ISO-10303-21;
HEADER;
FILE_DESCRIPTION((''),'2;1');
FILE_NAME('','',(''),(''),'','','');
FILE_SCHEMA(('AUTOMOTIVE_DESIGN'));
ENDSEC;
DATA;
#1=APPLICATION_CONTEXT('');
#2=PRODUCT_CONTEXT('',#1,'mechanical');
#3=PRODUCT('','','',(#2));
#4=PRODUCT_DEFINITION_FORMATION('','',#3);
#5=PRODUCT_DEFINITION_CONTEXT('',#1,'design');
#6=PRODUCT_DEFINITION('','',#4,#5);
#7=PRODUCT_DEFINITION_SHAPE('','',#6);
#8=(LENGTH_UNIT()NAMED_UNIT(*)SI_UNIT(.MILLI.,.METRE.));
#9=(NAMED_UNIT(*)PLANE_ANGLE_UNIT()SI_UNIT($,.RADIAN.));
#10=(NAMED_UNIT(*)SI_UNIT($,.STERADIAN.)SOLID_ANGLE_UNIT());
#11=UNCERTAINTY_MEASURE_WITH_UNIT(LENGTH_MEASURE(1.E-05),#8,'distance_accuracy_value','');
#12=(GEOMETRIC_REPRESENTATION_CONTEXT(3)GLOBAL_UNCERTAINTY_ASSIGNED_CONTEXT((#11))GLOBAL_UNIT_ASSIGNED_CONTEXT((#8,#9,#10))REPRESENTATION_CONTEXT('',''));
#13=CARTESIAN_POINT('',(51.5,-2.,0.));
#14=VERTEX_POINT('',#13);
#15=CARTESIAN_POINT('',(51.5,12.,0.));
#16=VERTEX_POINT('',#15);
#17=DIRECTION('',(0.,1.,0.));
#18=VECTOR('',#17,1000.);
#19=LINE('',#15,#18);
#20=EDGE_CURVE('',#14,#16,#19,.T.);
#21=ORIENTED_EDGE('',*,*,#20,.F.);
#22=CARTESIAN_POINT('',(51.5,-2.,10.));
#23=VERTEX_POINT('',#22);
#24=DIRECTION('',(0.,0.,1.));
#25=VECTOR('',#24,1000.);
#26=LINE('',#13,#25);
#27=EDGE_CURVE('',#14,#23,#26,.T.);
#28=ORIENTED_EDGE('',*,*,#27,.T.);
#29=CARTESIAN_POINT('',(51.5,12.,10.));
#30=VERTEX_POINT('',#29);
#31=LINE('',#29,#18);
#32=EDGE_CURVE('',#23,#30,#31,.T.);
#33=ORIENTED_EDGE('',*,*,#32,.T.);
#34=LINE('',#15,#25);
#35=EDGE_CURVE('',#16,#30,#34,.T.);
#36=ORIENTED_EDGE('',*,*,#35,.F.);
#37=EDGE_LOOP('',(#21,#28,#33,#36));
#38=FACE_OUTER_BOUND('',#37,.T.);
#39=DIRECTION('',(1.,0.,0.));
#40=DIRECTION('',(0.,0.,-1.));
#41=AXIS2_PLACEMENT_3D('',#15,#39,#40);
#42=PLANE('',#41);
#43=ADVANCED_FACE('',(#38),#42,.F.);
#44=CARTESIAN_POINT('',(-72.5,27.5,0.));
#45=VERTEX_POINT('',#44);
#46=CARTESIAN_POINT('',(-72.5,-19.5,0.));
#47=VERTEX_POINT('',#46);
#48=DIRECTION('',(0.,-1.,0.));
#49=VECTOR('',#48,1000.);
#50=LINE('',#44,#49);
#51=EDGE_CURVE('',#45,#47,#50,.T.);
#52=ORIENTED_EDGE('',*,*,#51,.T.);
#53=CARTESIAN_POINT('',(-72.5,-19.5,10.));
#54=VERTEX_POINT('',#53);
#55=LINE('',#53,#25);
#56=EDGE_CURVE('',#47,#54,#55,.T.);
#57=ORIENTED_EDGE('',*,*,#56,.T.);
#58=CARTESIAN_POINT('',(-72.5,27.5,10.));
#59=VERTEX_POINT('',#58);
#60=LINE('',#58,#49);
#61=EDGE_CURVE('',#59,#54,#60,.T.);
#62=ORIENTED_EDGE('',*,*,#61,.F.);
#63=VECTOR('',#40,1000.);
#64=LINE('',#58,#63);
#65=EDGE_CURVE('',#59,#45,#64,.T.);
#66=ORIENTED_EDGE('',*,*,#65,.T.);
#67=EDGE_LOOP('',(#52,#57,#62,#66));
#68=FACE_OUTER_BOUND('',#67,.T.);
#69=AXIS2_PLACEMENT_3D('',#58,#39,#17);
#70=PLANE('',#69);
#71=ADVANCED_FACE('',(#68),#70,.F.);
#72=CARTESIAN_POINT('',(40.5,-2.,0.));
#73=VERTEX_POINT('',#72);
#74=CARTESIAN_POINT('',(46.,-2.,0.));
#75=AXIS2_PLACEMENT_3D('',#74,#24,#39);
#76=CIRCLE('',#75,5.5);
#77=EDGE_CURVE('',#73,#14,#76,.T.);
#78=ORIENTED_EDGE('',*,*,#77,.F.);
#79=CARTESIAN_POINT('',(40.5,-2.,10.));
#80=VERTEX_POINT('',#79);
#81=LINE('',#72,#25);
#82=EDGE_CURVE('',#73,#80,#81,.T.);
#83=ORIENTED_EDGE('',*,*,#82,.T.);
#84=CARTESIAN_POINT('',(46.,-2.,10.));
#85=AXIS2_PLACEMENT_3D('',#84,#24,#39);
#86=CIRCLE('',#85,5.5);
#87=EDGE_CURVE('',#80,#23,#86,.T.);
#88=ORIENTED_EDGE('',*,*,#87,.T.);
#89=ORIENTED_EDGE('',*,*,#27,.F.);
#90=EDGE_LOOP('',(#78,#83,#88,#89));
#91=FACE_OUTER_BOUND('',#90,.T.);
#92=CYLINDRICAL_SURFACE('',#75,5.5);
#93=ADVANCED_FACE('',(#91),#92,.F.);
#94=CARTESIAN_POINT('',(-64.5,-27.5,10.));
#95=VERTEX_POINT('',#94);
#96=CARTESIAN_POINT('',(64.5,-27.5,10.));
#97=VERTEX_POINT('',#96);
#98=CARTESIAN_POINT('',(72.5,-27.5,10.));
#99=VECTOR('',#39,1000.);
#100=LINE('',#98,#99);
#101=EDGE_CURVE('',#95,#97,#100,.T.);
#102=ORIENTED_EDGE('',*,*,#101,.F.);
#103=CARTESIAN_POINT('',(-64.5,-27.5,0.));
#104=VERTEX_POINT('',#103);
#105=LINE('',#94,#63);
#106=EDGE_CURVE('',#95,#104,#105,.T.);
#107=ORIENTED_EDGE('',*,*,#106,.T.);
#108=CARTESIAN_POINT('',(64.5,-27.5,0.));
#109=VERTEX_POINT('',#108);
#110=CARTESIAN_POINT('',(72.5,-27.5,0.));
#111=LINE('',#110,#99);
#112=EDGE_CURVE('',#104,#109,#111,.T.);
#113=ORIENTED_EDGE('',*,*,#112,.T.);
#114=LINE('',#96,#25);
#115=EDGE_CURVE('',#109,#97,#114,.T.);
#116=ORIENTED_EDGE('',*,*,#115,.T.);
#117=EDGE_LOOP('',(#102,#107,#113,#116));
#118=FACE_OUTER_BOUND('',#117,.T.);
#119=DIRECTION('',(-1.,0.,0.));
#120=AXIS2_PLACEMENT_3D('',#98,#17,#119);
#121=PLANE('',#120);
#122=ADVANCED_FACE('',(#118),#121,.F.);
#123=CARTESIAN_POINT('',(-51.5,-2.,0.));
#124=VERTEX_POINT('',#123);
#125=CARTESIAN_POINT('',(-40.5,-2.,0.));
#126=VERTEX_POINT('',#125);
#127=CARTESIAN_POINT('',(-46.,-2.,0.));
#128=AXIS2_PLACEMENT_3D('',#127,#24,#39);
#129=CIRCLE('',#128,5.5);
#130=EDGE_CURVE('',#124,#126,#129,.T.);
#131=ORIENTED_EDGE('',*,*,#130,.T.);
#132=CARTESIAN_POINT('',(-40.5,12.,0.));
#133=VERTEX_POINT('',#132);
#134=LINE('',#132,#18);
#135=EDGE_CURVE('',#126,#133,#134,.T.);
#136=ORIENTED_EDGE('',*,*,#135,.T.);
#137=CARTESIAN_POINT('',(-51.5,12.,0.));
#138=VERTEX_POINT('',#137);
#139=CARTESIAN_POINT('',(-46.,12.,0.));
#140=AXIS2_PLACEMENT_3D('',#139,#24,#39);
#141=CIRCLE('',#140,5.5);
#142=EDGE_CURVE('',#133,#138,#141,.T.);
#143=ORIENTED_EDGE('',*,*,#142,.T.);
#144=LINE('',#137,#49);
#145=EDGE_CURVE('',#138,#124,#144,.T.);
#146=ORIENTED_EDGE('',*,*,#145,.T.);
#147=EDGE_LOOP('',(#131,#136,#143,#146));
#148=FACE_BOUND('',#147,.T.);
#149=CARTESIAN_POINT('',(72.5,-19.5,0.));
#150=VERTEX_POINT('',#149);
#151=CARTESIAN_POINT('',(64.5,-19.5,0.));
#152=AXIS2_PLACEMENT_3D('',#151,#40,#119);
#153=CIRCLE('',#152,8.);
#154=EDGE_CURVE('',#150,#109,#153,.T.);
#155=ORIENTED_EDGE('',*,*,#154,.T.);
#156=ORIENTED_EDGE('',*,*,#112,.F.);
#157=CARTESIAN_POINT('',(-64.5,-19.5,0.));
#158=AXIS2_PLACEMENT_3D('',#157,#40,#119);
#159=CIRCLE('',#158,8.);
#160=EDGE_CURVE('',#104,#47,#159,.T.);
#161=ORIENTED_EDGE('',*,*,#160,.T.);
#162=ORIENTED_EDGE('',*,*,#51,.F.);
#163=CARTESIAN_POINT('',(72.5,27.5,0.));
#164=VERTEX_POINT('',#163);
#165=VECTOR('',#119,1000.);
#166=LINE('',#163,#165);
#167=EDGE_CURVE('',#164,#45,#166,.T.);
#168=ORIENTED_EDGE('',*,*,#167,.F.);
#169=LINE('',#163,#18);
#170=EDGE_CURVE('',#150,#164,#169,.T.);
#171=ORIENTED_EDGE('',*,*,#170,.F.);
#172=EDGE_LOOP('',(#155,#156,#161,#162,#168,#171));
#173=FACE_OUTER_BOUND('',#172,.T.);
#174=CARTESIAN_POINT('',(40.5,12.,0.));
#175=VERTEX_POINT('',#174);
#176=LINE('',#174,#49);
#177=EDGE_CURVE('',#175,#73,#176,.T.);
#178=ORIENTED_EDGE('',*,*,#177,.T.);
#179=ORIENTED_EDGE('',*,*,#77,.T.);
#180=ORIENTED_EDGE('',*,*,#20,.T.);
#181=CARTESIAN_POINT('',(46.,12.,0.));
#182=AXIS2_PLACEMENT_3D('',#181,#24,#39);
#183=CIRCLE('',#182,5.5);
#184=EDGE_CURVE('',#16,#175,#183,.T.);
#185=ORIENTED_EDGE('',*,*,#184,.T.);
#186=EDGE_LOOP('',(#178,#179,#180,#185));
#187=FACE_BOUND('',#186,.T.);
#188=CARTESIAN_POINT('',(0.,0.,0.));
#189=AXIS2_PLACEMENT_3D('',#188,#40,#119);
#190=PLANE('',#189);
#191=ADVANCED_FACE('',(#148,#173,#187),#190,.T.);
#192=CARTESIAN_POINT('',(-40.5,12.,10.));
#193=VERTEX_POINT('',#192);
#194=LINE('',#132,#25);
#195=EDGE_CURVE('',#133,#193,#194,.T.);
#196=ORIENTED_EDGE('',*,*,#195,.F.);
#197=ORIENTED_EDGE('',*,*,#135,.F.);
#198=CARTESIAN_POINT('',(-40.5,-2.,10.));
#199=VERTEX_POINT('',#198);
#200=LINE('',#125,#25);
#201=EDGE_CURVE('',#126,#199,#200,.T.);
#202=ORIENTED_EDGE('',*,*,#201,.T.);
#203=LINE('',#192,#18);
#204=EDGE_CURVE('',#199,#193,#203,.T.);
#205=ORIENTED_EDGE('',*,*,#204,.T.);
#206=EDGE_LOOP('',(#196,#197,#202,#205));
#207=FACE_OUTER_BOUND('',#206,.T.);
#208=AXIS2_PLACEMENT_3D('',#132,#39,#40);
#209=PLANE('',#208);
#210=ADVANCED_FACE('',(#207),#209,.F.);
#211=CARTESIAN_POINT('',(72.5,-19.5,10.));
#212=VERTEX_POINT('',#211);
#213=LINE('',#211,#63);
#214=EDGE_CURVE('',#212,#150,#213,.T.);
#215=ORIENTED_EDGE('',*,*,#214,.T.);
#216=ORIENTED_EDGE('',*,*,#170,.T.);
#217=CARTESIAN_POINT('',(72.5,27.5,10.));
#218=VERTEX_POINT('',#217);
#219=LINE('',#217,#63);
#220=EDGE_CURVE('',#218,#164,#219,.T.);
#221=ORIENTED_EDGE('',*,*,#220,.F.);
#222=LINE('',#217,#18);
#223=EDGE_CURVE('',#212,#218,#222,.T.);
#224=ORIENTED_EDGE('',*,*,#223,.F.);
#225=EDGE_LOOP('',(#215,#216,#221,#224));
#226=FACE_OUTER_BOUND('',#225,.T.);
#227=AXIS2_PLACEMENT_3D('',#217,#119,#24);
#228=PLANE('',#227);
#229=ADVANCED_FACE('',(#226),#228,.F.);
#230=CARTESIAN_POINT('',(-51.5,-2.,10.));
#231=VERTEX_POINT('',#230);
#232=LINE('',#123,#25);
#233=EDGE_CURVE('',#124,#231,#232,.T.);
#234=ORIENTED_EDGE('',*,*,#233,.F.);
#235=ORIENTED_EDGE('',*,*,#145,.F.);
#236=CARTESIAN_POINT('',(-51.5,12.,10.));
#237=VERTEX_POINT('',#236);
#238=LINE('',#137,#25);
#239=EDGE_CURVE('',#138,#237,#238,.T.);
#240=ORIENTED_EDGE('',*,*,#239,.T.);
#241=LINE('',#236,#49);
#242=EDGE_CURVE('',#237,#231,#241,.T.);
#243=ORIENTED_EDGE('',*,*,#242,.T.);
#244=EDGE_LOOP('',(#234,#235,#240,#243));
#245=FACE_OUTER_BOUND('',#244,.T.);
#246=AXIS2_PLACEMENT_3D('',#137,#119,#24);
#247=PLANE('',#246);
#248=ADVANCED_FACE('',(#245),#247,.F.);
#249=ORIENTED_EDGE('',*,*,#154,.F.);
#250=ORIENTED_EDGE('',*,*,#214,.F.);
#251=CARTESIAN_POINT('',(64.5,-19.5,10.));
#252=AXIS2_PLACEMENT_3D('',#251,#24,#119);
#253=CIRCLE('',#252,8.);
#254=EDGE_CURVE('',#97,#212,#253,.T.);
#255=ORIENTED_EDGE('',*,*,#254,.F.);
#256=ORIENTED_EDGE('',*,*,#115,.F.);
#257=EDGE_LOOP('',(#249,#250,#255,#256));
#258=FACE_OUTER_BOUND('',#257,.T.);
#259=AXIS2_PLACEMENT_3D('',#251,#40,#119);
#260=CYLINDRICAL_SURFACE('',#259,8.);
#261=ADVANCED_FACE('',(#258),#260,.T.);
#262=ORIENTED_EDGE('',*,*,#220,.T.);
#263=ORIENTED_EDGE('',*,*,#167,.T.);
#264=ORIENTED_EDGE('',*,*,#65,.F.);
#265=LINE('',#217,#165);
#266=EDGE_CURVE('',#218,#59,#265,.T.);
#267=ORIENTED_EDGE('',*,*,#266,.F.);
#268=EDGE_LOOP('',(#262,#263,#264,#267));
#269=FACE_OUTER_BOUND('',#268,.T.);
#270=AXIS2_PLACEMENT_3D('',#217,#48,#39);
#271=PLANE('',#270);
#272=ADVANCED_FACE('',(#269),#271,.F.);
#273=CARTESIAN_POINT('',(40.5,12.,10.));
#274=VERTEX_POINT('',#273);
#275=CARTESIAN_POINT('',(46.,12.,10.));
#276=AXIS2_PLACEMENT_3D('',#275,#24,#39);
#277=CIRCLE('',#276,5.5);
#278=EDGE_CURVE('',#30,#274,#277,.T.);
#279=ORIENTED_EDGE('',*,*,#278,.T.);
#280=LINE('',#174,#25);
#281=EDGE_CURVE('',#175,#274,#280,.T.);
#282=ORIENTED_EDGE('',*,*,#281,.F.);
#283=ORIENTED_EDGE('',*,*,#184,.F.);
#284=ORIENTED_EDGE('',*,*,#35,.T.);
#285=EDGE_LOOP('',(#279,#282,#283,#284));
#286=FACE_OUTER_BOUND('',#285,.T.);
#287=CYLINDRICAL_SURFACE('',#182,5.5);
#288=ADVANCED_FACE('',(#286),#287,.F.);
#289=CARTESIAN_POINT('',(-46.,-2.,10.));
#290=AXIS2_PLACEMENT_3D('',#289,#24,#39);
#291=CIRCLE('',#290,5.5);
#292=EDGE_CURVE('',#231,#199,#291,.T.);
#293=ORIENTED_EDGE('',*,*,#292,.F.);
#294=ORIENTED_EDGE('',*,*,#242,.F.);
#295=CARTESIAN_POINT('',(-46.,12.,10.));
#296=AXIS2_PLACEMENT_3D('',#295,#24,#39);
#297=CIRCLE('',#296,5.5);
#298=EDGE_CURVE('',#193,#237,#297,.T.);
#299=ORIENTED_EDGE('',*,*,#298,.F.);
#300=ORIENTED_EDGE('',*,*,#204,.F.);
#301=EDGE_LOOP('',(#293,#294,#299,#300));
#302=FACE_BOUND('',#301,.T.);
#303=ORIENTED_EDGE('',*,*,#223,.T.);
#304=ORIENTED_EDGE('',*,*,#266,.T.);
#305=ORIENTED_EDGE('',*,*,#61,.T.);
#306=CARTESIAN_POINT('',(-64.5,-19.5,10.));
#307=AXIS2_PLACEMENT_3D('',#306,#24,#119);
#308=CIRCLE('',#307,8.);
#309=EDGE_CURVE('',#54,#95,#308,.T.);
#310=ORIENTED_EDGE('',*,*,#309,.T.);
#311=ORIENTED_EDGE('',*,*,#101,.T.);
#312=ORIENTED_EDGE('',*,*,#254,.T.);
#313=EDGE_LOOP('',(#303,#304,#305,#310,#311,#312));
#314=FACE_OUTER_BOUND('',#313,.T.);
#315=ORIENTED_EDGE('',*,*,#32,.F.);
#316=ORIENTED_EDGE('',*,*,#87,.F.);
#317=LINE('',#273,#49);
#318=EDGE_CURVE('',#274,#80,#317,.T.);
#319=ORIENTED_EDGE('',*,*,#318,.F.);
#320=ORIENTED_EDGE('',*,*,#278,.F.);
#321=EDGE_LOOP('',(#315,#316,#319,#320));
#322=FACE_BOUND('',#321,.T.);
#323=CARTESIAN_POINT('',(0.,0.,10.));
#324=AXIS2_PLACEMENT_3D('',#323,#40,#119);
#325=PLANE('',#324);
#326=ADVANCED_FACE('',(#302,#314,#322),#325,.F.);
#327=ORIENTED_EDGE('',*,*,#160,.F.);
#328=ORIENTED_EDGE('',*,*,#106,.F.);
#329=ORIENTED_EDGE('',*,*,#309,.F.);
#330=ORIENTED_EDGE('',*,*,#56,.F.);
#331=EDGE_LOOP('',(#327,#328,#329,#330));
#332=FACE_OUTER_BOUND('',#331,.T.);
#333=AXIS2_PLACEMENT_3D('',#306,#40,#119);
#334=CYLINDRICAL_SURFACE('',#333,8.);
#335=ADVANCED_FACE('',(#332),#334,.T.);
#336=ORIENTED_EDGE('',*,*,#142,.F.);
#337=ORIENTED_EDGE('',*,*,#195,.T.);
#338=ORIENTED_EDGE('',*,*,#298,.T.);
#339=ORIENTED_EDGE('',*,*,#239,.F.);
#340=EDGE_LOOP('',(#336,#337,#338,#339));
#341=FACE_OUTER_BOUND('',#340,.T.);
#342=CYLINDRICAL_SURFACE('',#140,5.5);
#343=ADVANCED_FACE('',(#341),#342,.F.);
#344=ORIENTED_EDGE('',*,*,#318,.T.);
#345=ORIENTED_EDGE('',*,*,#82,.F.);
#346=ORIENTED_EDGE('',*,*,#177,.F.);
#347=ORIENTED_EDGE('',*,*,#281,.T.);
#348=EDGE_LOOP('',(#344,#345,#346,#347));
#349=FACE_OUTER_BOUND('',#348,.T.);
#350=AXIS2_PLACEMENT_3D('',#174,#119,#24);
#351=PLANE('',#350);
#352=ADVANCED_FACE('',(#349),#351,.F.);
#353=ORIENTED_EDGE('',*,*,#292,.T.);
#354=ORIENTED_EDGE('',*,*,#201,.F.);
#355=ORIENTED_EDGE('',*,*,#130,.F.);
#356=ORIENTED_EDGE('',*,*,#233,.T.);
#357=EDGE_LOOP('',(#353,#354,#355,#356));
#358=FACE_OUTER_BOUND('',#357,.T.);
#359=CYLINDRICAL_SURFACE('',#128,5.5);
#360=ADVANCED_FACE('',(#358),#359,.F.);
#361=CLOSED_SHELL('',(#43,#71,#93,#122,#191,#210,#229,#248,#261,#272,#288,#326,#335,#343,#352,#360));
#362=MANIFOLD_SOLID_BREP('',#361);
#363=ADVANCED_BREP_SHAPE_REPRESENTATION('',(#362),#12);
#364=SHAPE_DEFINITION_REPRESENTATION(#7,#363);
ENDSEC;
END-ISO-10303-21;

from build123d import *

# Parameters (mm, degrees)
SKETCH_1_W          = 145
SKETCH_1_H          = 55
EXTRUDE_1_DEPTH     = 10
FILLET_1_R          = 8
CUT_EXTRUDE_1_DEPTH = 10


with BuildPart() as part:
    # 草图1 → 凸台-拉伸1 (new body)
    with BuildSketch(Plane.XY):
        Rectangle(SKETCH_1_W, SKETCH_1_H)
    extrude(amount=EXTRUDE_1_DEPTH)

    # 圆角1
    fillet_1_edges = [part.edges().sort_by_distance(p)[0] for p in [
        (72.5, -27.5, 5),
        (-72.5, -27.5, 5),
    ]]
    fillet(fillet_1_edges, radius=FILLET_1_R)

    # 草图2 → 切除-拉伸1 (cut)
    with BuildSketch(Plane.XY.offset(10)):
        with BuildLine():
            Line((51.5, 12), (51.5, -2))
            ThreePointArc((51.5, -2), (46, -7.5), (40.5, -2))
            Line((40.5, -2), (40.5, 12))
            ThreePointArc((40.5, 12), (46, 17.5), (51.5, 12))
        make_face()
        with BuildLine():
            Line((-40.5, 12), (-40.5, -2))
            ThreePointArc((-40.5, -2), (-46, -7.5), (-51.5, -2))
            Line((-51.5, -2), (-51.5, 12))
            ThreePointArc((-51.5, 12), (-46, 17.5), (-40.5, 12))
        make_face()
    extrude(amount=-CUT_EXTRUDE_1_DEPTH, mode=Mode.SUBTRACT)


solid = part.part
